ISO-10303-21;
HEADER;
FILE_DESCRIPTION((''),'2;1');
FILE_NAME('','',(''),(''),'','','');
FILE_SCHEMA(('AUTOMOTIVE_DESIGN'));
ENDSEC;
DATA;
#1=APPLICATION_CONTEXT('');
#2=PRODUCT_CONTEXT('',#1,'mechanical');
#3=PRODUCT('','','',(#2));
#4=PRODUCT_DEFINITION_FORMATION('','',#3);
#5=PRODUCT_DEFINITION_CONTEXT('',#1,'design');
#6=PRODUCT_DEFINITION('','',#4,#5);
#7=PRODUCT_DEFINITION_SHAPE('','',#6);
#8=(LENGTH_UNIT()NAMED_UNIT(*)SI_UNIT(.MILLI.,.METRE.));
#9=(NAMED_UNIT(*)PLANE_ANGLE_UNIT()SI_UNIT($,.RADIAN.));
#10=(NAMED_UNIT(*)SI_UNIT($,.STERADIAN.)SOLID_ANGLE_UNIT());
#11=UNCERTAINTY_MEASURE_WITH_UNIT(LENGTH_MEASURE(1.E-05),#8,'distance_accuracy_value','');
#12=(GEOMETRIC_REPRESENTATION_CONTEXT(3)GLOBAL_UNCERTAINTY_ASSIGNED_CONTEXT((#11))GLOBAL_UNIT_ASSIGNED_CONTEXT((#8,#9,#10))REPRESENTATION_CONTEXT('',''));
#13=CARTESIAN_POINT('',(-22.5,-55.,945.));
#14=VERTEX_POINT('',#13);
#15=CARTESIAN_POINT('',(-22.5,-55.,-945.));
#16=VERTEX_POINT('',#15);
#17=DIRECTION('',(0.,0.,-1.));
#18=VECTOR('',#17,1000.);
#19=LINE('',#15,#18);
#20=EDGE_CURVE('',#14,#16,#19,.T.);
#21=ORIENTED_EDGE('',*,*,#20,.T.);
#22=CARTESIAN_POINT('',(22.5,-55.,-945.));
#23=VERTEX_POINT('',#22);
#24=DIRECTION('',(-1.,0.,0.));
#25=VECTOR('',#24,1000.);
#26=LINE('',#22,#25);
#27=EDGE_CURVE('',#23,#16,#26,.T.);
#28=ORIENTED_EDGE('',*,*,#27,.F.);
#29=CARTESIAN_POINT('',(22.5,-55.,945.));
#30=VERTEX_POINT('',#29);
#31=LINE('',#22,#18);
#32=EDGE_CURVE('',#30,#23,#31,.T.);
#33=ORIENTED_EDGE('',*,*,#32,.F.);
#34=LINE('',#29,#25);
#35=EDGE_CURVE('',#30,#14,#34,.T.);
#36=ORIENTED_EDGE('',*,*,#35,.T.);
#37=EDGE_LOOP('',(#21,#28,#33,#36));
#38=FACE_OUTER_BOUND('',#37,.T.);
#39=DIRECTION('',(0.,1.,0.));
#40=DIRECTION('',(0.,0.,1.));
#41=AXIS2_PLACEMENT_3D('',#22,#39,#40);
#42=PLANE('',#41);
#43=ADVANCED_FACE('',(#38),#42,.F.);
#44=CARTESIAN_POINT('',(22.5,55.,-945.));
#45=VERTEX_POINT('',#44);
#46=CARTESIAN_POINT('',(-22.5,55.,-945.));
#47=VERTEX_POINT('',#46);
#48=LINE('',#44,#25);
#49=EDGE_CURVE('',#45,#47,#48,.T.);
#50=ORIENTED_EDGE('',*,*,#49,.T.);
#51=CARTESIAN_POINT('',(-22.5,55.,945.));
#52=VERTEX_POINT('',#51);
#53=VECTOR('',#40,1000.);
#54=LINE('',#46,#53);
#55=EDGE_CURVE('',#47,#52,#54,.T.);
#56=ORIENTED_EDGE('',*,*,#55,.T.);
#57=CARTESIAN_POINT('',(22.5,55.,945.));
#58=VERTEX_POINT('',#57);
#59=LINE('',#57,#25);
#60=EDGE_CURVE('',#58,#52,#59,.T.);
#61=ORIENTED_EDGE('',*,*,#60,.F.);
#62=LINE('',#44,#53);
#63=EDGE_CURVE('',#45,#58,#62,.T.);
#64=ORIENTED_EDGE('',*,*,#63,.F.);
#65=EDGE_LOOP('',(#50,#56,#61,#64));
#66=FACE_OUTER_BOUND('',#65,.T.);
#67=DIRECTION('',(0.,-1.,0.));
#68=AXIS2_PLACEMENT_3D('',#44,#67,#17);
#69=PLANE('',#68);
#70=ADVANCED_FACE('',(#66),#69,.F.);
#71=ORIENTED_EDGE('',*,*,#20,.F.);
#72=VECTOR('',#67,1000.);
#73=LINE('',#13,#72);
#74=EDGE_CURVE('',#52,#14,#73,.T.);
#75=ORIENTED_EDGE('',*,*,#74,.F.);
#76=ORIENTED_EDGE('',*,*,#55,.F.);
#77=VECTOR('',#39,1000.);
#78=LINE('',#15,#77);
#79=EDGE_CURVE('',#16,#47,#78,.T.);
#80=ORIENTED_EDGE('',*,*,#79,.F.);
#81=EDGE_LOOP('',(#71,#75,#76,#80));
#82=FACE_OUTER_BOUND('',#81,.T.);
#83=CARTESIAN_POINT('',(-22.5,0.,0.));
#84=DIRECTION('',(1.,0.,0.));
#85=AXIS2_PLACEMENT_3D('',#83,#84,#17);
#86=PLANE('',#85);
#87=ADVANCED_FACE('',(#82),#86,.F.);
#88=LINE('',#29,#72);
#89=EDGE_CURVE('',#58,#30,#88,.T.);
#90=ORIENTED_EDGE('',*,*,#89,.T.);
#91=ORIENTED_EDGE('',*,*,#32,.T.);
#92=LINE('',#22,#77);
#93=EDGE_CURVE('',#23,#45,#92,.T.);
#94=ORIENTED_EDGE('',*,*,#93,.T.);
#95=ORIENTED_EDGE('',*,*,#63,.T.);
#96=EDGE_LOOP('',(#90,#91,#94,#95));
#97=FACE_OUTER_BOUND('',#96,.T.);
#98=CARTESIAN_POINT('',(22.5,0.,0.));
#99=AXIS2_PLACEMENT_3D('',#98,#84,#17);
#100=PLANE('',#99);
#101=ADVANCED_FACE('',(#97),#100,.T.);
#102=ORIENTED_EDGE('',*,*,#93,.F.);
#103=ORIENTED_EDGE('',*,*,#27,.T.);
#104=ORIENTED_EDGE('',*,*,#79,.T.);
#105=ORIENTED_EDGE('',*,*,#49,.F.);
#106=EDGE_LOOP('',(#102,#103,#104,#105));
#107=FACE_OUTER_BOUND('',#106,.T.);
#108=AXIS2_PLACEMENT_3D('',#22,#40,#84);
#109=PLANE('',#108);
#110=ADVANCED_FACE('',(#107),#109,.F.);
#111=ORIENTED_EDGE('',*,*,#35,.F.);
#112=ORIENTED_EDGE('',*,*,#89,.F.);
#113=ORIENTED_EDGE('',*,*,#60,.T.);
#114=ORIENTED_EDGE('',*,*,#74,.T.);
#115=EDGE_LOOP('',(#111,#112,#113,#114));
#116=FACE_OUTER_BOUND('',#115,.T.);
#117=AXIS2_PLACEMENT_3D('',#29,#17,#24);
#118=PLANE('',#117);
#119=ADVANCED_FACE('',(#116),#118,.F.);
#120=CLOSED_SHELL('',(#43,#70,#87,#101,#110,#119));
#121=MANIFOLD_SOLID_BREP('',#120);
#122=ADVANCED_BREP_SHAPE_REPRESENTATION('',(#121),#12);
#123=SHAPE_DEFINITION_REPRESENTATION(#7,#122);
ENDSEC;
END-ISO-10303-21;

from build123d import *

# Parameters (mm, degrees)
SKETCH1_W           = 1890
SKETCH1_H           = 110
BOSS_EXTRUDE1_DEPTH = 22.5


with BuildPart() as part:
    # Sketch1 → Boss-Extrude1 (new, symmetric)
    with BuildSketch(Plane(origin=(0, 0, 0), x_dir=(0, 0, -1), z_dir=(1, 0, 0))):
        Rectangle(SKETCH1_W, SKETCH1_H)
    extrude(amount=BOSS_EXTRUDE1_DEPTH, both=True)


solid = part.part
